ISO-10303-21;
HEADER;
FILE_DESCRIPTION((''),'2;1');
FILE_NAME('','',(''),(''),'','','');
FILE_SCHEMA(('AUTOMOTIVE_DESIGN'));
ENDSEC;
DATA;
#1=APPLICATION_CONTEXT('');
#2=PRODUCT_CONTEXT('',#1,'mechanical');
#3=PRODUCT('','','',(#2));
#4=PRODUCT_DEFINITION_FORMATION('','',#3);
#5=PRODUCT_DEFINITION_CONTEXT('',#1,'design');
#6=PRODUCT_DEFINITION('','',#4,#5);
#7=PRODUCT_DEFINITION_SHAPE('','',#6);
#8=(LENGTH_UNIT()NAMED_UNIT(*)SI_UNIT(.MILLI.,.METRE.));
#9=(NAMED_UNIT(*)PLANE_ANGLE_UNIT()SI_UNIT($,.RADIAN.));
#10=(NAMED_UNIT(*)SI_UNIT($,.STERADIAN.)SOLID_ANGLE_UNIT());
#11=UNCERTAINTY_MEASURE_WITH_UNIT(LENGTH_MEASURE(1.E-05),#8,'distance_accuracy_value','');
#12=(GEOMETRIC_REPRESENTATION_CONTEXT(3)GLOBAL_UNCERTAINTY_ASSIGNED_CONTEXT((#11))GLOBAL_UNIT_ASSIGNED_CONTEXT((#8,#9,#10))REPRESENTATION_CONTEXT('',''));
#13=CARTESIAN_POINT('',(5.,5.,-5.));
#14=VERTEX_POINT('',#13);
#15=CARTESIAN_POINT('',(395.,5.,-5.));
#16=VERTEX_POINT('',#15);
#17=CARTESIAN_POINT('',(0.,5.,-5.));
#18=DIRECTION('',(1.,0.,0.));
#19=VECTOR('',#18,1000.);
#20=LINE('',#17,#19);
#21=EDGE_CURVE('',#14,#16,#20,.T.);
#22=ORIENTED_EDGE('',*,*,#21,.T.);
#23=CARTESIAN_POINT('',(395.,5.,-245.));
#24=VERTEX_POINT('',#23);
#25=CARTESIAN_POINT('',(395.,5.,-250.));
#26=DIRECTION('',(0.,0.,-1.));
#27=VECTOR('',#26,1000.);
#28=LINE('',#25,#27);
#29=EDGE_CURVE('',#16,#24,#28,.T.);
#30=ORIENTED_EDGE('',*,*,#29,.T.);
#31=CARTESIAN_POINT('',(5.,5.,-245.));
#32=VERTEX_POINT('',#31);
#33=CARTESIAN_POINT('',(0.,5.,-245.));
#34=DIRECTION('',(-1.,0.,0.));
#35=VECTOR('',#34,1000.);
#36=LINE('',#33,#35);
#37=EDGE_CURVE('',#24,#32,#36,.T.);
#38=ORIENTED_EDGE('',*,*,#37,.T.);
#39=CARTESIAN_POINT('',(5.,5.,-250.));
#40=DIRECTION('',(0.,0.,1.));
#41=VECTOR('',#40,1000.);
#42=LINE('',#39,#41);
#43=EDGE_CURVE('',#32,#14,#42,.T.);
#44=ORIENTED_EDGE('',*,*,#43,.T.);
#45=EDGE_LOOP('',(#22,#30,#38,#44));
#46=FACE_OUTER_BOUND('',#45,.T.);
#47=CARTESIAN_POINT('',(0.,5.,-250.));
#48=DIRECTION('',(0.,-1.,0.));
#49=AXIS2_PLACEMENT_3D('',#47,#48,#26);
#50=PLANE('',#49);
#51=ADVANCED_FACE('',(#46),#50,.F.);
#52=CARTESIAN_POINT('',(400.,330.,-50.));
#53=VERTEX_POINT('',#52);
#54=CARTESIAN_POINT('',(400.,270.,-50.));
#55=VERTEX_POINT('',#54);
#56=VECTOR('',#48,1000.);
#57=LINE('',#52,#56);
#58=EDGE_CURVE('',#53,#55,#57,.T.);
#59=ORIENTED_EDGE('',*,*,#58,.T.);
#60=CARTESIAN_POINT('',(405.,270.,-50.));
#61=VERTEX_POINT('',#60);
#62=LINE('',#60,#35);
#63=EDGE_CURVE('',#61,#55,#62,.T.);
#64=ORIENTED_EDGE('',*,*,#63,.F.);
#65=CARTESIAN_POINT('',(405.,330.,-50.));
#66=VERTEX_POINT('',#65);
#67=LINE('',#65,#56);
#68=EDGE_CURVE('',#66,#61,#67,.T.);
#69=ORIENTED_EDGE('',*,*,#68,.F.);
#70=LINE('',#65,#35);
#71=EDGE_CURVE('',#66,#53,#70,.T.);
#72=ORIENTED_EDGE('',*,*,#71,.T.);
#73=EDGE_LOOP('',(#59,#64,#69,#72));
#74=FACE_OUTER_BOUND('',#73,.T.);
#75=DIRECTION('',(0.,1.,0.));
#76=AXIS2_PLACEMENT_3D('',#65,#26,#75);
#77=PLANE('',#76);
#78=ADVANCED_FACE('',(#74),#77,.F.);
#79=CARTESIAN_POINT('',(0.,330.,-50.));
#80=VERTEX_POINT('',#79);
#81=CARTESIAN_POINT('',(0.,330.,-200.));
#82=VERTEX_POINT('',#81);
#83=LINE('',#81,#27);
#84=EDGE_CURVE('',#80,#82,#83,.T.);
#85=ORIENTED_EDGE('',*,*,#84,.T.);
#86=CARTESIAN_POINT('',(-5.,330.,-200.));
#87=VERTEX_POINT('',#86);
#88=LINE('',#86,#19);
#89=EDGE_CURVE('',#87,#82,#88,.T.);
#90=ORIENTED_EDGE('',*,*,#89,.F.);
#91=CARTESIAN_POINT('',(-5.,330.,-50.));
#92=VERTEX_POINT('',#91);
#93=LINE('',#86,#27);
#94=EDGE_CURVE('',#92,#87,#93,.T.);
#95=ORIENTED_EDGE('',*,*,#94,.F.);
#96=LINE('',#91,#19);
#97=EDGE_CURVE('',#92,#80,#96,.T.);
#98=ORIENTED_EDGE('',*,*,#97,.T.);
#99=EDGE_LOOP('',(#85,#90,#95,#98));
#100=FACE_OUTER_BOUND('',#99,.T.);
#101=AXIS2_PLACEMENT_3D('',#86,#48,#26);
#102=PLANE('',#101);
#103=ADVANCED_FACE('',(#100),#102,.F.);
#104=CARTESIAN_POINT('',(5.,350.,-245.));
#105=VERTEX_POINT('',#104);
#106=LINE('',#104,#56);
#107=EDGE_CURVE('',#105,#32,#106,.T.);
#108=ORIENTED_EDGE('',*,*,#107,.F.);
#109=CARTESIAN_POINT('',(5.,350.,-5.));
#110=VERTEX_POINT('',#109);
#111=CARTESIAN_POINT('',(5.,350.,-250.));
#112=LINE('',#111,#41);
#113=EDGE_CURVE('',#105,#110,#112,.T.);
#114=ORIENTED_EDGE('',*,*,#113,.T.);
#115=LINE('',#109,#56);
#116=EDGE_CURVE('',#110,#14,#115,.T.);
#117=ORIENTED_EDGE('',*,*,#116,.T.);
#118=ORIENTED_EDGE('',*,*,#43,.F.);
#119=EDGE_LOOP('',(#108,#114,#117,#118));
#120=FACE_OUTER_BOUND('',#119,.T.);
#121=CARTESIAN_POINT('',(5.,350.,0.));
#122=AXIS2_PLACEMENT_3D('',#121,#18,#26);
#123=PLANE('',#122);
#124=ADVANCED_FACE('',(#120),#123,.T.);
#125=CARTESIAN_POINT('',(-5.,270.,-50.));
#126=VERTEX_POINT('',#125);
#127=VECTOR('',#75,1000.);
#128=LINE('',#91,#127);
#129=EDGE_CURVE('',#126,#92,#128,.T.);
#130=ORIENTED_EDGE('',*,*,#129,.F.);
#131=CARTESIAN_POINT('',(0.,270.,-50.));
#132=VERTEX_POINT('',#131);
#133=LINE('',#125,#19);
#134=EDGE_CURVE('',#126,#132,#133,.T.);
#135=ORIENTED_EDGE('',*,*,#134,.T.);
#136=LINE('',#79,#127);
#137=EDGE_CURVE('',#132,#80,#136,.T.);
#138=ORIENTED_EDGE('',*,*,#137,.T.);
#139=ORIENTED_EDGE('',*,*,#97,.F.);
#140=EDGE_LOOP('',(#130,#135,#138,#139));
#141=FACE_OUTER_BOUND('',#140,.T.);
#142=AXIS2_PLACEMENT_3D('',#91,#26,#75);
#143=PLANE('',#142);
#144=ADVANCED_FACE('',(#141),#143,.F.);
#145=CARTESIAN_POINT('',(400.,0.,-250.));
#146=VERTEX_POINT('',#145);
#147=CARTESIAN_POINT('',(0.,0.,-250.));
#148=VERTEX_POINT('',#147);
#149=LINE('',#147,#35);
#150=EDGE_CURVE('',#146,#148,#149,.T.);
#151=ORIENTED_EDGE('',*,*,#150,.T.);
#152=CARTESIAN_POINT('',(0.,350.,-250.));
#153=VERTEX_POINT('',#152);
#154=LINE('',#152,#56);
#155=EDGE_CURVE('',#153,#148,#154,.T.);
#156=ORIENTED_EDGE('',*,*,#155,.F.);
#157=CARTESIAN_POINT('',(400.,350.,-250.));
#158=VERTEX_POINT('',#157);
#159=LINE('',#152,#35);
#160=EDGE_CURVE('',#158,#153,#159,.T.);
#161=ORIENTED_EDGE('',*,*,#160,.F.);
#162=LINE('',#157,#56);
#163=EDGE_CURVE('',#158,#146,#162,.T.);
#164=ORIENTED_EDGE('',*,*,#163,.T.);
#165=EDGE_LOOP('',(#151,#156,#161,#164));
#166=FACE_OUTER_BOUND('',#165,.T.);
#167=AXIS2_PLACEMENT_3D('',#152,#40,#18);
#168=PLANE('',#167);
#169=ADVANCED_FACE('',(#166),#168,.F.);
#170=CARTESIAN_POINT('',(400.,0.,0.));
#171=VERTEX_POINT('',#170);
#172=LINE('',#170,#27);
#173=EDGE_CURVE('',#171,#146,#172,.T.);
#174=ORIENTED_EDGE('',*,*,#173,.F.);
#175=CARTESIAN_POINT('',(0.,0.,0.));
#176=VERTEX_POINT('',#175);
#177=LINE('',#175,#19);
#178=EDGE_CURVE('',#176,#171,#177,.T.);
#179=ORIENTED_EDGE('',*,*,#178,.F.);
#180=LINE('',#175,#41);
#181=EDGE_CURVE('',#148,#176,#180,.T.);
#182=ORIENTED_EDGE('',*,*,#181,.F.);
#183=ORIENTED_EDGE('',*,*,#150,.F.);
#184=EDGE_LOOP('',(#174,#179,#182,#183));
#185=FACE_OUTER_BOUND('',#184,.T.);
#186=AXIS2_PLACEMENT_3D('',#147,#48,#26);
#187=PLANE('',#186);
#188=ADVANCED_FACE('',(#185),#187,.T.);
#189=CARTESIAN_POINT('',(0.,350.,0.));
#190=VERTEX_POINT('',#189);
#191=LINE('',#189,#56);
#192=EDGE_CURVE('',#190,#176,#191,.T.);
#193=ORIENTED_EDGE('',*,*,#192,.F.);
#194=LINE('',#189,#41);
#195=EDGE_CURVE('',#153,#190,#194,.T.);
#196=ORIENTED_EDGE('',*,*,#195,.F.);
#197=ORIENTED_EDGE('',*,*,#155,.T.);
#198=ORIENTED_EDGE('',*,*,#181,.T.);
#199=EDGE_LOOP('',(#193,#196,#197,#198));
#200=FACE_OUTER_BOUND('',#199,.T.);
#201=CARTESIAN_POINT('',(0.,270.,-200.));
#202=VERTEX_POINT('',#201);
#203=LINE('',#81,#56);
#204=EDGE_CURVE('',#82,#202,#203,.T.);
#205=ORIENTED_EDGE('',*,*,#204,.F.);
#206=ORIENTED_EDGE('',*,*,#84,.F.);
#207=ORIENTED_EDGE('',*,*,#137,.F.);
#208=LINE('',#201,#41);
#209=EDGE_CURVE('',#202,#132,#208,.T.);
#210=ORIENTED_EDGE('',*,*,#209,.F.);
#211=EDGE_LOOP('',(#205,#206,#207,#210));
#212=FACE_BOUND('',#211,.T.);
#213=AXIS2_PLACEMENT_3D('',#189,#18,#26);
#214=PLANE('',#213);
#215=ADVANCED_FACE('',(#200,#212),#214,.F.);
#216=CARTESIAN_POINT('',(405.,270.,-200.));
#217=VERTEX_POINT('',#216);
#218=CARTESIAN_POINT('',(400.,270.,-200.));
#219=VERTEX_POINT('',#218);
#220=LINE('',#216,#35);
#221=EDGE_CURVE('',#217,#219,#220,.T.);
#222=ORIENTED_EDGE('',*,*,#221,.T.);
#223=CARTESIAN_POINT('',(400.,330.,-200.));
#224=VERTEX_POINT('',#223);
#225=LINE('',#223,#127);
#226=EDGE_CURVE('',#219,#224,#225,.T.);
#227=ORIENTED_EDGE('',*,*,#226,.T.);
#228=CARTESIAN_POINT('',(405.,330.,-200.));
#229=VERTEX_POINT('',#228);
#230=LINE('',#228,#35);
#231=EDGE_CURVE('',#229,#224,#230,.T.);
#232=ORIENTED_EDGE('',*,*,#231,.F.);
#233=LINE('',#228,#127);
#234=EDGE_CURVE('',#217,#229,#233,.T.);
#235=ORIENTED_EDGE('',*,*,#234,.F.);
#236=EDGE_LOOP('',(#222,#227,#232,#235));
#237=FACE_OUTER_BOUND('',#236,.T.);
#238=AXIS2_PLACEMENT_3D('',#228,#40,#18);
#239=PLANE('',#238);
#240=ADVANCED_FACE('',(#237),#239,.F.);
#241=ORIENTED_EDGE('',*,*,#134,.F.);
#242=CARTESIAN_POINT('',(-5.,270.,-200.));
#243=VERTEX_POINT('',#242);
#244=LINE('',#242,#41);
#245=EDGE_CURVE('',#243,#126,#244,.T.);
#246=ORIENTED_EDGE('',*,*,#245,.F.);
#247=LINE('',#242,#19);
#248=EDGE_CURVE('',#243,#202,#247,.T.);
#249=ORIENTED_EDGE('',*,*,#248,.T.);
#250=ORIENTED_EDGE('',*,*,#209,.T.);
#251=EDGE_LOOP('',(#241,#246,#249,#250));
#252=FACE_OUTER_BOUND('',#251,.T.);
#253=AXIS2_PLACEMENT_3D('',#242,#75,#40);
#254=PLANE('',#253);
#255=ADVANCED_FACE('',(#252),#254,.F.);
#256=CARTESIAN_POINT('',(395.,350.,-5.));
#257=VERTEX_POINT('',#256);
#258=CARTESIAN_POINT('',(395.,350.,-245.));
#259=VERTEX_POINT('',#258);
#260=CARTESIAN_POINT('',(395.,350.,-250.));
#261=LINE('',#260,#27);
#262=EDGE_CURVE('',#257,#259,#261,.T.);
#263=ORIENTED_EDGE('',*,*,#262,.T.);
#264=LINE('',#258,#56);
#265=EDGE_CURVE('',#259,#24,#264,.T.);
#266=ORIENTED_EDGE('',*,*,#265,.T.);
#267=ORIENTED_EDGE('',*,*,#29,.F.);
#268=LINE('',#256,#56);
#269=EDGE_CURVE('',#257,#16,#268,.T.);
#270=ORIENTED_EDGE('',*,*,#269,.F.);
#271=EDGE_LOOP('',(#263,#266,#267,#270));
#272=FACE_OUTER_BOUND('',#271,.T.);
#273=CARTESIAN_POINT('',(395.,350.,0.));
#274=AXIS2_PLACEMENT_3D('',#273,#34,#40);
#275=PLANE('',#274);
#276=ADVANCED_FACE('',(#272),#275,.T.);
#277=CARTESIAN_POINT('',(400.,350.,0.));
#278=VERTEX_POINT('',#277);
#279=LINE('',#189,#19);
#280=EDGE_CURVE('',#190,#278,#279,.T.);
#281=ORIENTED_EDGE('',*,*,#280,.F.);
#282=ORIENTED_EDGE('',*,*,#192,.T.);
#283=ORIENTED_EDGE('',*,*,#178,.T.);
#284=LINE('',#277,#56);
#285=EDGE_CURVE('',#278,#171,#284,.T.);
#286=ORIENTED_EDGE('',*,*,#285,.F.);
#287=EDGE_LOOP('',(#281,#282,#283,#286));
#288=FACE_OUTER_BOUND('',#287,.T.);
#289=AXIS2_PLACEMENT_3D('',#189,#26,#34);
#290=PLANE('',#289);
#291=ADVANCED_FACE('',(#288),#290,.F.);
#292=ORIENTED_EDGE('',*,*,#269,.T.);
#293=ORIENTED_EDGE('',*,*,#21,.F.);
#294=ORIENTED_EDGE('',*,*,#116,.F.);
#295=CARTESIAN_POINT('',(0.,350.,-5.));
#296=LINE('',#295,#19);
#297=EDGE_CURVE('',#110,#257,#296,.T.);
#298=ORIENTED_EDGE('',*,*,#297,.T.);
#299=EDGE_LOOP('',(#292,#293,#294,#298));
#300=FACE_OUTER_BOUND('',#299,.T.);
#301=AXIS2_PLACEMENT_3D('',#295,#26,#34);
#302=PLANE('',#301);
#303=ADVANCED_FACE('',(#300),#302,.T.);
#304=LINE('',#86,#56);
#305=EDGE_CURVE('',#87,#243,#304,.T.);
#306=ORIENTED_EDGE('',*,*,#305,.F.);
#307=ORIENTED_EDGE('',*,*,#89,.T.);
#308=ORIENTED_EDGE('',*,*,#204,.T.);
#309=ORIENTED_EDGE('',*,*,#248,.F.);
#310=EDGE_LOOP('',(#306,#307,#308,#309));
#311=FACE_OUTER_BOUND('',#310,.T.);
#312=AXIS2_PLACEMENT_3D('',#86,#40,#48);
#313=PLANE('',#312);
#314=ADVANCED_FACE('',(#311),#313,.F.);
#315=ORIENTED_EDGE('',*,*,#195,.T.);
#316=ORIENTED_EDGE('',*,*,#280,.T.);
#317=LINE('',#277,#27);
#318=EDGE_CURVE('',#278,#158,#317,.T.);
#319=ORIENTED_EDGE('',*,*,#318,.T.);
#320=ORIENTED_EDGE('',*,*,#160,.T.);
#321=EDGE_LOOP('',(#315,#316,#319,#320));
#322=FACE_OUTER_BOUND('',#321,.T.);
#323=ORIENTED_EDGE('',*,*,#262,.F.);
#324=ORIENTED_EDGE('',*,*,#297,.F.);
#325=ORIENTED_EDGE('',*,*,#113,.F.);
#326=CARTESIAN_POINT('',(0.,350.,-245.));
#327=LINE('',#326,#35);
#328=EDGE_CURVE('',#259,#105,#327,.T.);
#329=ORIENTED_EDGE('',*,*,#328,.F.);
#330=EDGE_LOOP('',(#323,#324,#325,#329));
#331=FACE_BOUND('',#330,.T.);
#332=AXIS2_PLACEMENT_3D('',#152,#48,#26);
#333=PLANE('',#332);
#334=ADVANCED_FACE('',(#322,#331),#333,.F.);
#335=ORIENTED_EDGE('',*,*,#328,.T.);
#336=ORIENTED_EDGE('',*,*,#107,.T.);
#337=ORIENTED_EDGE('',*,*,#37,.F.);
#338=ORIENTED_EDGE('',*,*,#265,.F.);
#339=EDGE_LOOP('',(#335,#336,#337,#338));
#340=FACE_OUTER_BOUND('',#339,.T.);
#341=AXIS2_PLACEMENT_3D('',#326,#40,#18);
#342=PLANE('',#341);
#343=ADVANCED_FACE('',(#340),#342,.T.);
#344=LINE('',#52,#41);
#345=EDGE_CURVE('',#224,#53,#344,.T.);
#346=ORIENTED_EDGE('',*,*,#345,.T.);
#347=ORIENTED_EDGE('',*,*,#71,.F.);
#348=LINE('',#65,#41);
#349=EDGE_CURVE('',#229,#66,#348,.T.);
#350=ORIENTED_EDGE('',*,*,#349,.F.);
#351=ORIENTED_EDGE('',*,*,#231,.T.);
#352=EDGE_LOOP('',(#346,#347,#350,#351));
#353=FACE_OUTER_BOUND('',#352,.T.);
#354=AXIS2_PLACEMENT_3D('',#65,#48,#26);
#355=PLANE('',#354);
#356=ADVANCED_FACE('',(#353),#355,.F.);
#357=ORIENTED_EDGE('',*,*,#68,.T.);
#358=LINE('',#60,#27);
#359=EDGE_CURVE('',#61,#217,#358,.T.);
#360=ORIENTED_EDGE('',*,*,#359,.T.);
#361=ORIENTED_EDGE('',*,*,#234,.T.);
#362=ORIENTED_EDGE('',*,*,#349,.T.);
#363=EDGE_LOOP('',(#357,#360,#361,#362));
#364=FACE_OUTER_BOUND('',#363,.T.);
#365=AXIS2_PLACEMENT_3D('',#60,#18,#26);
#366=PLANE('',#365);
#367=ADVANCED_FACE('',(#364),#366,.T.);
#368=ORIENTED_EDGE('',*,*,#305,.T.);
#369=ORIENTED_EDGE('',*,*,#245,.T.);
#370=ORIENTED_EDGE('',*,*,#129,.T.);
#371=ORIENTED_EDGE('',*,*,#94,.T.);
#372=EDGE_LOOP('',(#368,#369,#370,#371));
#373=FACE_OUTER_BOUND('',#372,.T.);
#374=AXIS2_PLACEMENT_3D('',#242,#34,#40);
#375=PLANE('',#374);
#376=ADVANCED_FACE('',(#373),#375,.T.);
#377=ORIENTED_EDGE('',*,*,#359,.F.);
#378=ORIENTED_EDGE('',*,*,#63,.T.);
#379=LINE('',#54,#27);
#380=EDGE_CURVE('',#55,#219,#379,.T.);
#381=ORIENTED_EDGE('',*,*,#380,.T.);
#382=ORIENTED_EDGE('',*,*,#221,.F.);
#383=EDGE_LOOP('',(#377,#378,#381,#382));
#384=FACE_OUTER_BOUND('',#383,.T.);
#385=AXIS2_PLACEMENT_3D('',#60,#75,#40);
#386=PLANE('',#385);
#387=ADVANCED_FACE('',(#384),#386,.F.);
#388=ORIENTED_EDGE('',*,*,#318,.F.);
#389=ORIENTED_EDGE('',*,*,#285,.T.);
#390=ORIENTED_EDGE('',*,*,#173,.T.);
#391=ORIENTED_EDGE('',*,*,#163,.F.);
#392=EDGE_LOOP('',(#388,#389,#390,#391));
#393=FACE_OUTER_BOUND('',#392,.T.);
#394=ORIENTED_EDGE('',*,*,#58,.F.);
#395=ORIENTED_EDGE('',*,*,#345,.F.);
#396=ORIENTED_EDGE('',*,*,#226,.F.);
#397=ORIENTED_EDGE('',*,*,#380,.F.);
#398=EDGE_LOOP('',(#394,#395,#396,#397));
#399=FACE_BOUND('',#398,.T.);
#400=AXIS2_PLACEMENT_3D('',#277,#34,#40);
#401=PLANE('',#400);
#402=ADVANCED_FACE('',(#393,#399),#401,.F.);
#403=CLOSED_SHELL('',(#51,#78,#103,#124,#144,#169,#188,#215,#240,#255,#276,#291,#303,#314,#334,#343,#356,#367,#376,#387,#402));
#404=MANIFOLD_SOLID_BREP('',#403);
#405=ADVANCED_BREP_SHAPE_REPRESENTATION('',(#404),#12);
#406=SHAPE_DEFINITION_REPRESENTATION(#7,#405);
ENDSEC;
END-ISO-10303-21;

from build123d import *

# Parameters (mm, degrees)
SKETCH_1_W      = 400
SKETCH_1_H      = 250
EXTRUDE_1_DEPTH = 350
SHELL_1_T       = -5
SKETCH_2_W      = 150
SKETCH_2_H      = 60
EXTRUDE_2_DEPTH = 5
SKETCH_3_W      = 150
SKETCH_3_H      = 60
EXTRUDE_3_DEPTH = 5


with BuildPart() as part:
    # 草图1 → 凸台-拉伸1 (new body)
    with BuildSketch(Plane(origin=(0, 0, 0), x_dir=(1, 0, 0), z_dir=(0, 1, 0))):
        with Locations((200, 125)):
            Rectangle(SKETCH_1_W, SKETCH_1_H)
    extrude(amount=EXTRUDE_1_DEPTH)

    # 抽壳1
    shell_1_openings = [part.faces().sort_by_distance(p)[0] for p in [
        (200, 350, -125),
    ]]
    offset(amount=SHELL_1_T, openings=shell_1_openings, kind=Kind.INTERSECTION)

    # 草图2 → 凸台-拉伸2 (add)
    with BuildSketch(Plane(origin=(400, 0, 0), x_dir=(0, 0, -1), z_dir=(1, 0, 0))):
        with Locations((125, 300)):
            Rectangle(SKETCH_2_W, SKETCH_2_H)
    extrude(amount=EXTRUDE_2_DEPTH)

    # 草图3 → 凸台-拉伸3 (add)
    with BuildSketch(Plane.ZY):
        with Locations((-125, 300)):
            Rectangle(SKETCH_3_W, SKETCH_3_H)
    extrude(amount=EXTRUDE_3_DEPTH)


solid = part.part
